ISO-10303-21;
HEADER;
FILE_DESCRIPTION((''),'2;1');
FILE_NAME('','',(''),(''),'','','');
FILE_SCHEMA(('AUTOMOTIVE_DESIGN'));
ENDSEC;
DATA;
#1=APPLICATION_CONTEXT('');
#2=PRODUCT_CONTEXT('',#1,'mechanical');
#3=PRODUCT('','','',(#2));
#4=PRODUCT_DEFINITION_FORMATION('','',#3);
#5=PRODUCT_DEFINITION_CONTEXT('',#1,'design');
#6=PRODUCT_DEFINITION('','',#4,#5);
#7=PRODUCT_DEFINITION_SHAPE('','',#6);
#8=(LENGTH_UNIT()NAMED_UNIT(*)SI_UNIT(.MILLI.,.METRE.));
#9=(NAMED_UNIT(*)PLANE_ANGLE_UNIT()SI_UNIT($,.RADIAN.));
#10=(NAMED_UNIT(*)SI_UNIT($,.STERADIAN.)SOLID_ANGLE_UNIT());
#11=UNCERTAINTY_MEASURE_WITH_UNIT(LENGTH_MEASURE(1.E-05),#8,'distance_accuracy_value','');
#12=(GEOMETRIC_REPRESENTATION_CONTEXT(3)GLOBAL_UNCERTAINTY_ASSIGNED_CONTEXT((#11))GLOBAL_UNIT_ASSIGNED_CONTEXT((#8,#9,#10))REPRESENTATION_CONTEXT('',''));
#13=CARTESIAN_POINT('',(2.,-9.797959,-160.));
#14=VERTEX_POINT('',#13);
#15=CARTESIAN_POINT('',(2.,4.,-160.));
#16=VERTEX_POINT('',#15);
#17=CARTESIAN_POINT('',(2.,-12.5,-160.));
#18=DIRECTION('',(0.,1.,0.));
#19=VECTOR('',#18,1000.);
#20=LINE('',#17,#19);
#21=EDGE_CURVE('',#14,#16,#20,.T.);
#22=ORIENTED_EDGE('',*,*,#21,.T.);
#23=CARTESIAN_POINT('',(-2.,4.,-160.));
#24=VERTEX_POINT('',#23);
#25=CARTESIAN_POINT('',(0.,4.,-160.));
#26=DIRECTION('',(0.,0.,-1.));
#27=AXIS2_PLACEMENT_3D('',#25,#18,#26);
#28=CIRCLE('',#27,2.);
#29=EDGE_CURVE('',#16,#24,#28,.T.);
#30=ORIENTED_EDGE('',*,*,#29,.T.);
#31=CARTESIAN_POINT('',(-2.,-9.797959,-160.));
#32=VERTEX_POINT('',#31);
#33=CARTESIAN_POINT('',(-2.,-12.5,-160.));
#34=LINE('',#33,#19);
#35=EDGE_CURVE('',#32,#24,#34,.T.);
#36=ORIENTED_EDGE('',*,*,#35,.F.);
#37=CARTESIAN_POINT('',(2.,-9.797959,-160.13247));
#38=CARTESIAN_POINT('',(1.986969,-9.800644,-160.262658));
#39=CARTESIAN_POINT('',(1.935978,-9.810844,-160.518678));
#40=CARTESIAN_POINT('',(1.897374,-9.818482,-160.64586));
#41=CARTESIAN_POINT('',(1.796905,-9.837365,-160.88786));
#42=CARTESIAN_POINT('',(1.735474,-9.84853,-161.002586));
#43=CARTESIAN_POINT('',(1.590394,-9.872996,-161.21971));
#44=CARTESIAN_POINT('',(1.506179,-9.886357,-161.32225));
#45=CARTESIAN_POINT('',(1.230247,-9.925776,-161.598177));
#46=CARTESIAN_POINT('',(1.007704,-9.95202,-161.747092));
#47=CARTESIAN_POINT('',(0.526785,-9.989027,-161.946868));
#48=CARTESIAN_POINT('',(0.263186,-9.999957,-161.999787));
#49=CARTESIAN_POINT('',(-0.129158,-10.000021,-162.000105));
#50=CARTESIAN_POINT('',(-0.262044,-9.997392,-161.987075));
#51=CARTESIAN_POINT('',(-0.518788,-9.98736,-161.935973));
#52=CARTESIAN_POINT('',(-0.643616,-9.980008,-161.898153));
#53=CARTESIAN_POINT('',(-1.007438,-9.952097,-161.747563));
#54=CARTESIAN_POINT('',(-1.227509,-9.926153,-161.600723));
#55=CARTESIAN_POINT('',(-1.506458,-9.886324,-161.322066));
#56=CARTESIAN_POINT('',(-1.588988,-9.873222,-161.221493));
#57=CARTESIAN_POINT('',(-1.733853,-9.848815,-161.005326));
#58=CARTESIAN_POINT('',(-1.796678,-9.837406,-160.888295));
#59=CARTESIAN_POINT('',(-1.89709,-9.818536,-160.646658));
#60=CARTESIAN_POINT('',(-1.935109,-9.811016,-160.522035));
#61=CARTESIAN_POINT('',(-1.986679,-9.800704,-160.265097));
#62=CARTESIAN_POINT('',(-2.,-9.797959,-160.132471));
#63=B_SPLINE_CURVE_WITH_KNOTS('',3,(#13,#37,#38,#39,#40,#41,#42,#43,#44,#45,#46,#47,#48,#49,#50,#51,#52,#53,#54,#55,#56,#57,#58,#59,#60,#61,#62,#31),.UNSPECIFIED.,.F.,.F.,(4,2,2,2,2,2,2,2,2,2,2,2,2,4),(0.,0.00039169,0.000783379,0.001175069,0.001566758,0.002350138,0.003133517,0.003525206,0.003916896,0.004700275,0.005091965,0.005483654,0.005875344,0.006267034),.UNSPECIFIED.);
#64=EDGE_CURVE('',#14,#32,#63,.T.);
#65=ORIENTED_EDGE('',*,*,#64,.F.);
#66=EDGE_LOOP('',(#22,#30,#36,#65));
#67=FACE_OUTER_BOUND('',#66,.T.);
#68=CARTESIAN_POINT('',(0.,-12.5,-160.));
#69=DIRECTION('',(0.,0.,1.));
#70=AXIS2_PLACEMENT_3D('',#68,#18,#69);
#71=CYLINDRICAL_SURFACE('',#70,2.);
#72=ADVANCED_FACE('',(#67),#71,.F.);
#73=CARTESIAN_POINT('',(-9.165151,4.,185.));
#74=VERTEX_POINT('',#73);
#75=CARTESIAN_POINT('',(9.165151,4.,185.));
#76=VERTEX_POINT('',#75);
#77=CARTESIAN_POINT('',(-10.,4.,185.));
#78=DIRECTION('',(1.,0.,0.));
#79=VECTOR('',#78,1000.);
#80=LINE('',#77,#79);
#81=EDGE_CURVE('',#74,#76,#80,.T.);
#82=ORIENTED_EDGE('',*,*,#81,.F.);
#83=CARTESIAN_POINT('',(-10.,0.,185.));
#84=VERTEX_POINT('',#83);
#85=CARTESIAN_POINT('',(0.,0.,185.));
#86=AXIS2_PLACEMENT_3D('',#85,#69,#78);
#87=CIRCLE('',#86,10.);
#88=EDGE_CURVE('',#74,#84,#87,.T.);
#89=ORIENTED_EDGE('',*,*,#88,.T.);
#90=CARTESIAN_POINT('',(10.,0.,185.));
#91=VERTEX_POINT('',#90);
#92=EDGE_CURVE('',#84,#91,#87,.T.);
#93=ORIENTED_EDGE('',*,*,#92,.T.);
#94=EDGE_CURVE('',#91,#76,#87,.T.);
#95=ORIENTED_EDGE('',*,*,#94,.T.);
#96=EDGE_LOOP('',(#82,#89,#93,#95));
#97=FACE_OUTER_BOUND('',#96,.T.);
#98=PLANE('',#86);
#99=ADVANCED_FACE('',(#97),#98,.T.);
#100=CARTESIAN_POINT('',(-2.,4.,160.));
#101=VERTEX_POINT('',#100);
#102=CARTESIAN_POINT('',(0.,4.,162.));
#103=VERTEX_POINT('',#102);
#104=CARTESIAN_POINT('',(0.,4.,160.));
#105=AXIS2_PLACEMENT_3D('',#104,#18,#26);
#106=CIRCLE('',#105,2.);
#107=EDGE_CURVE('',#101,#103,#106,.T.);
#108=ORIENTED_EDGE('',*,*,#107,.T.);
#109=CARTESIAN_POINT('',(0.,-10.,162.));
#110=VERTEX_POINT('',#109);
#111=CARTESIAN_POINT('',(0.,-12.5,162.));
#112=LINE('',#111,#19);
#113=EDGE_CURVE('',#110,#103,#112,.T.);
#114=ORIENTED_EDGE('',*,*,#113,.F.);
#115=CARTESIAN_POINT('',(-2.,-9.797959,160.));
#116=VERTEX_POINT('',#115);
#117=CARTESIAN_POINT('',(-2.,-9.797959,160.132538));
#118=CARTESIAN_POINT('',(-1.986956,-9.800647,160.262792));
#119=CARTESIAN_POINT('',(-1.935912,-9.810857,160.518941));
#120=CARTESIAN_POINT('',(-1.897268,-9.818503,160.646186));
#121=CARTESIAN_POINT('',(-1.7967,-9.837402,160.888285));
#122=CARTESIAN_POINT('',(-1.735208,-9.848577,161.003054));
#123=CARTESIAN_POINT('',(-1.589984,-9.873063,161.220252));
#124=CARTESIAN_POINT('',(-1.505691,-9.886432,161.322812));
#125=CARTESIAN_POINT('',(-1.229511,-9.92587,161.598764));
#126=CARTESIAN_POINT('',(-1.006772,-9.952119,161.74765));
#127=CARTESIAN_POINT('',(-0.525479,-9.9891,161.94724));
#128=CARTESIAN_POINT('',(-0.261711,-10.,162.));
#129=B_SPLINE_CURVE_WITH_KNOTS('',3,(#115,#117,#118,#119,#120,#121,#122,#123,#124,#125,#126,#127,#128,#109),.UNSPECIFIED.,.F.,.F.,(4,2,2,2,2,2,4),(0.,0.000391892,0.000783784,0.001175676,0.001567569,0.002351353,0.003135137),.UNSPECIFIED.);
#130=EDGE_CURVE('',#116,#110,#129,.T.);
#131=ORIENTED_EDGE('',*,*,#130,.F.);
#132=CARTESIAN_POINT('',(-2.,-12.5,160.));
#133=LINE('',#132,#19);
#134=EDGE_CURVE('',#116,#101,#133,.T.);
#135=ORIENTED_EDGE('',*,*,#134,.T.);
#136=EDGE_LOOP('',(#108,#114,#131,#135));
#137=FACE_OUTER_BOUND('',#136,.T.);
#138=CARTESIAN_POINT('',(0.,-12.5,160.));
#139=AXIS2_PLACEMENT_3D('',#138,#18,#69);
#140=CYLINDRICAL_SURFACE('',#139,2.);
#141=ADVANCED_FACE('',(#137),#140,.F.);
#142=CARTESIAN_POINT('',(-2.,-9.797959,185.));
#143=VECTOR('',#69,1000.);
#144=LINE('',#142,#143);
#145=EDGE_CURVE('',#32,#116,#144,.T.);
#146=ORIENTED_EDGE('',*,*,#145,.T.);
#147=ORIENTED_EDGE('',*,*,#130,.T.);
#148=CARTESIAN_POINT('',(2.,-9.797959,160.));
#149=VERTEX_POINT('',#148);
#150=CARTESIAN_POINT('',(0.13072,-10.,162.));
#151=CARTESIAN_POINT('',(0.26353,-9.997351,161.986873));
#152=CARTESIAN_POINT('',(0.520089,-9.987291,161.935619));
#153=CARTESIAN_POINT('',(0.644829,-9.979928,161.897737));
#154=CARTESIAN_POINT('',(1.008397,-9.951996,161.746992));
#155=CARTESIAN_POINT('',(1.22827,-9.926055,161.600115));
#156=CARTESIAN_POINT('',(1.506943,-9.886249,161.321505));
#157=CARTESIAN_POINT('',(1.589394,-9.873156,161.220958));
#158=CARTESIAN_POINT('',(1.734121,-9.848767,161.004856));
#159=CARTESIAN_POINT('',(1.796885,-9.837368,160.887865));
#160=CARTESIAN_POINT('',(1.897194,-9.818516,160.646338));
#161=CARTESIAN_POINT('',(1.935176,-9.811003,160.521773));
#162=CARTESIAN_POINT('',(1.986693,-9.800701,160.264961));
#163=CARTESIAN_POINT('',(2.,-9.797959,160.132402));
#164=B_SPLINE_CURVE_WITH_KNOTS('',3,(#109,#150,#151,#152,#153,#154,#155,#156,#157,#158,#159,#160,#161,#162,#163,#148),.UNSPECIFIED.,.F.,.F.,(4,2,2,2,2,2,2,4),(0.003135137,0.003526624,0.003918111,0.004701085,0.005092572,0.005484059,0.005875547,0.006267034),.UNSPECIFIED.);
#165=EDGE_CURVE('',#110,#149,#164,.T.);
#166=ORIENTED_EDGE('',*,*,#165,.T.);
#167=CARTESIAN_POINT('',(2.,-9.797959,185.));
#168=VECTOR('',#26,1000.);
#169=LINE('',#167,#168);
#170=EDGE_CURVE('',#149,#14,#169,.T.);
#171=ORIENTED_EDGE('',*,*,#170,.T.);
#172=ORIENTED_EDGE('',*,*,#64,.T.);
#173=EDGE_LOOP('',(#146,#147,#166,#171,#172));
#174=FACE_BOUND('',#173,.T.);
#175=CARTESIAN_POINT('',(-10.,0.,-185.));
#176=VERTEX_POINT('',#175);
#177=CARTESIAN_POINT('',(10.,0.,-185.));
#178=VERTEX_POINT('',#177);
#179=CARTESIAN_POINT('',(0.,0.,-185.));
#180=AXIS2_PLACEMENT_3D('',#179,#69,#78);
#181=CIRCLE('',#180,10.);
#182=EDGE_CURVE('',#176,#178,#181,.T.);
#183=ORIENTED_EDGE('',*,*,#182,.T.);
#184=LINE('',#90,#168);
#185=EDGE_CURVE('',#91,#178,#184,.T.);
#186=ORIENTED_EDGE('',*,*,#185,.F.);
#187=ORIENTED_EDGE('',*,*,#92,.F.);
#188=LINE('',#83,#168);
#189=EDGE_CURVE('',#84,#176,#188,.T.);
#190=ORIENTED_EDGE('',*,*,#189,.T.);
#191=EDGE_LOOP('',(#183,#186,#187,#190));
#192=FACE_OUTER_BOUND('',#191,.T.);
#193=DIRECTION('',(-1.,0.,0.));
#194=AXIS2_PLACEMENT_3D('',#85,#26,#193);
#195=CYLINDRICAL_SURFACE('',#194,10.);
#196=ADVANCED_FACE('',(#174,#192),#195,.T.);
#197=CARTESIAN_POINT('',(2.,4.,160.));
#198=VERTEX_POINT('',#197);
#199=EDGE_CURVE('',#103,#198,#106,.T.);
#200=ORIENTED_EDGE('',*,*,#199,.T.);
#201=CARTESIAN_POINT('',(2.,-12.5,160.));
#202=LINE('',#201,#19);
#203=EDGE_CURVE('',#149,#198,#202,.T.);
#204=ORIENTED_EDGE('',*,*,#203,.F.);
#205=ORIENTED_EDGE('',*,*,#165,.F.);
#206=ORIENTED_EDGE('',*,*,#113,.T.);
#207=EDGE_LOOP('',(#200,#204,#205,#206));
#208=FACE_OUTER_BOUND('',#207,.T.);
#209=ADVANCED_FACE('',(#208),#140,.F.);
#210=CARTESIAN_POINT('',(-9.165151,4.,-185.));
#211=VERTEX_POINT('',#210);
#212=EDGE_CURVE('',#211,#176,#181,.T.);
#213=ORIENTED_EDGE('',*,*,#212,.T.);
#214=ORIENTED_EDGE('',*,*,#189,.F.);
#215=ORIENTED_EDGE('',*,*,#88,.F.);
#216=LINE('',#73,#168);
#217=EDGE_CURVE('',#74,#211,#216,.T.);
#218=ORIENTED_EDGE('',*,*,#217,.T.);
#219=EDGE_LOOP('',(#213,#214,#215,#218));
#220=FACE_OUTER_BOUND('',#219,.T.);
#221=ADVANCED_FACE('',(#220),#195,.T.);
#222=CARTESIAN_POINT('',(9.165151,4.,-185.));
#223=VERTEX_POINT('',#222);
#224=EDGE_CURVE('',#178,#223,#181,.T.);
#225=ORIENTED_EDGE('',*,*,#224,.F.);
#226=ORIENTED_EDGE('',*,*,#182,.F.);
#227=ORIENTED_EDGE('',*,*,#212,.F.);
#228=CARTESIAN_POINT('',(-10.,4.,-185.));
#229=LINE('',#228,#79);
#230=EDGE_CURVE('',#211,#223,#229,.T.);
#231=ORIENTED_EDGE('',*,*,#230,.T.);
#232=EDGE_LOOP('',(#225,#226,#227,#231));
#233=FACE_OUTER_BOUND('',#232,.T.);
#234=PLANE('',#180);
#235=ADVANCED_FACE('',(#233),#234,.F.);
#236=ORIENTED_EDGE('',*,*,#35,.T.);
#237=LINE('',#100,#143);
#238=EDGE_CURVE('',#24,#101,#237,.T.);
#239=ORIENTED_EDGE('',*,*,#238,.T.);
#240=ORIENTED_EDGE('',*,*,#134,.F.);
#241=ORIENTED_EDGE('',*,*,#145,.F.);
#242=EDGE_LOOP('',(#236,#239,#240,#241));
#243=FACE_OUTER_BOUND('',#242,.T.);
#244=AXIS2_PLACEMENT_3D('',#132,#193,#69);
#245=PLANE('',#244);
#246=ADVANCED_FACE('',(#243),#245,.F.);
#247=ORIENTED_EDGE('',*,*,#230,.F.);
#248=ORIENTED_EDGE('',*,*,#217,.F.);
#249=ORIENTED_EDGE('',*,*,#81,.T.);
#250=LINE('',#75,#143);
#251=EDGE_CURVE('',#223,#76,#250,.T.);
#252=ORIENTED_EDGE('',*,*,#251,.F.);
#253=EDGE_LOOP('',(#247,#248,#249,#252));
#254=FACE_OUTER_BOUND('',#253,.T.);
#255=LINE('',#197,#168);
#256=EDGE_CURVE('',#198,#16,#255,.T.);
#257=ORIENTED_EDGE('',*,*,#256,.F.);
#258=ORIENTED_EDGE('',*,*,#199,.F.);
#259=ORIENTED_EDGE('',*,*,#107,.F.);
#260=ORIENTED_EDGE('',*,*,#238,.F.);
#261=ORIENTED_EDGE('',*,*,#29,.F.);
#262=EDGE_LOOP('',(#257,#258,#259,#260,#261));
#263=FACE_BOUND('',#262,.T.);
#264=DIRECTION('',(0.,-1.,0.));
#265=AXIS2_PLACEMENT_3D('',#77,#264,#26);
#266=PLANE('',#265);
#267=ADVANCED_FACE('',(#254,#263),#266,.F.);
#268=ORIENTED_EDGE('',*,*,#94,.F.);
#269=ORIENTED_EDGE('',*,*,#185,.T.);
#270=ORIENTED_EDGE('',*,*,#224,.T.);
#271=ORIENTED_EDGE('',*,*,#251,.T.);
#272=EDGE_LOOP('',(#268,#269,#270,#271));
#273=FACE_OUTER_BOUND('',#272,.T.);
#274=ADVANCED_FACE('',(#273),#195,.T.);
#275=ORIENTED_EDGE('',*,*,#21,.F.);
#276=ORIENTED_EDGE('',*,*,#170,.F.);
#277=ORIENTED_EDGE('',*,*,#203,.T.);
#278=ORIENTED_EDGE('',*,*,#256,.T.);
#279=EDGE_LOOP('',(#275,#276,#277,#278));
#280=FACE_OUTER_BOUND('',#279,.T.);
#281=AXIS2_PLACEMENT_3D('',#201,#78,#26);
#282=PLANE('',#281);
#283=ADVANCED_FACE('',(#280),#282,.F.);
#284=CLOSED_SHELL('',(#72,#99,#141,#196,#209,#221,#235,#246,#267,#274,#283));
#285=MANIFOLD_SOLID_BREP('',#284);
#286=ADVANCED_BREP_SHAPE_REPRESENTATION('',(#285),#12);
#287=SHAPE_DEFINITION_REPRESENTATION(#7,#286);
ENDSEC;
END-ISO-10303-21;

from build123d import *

# Parameters (mm, degrees)
SKETCH_3_R          = 10
EXTRUDE_3_DEPTH     = 185
CUT_EXTRUDE_1_DEPTH = 12.5
SKETCH_5_W          = 370
SKETCH_5_H          = 20
CUT_EXTRUDE_2_DEPTH = 10


with BuildPart() as part:
    # 草图3 → 凸台-拉伸3 (new, symmetric)
    with BuildSketch(Plane.XY):
        Circle(SKETCH_3_R)
    extrude(amount=EXTRUDE_3_DEPTH, both=True)

    # 草图4 → 切除-拉伸1 (cut, symmetric)
    with BuildSketch(Plane(origin=(0, 0, 0), x_dir=(1, 0, 0), z_dir=(0, 1, 0))):
        with BuildLine():
            Line((-2, -160), (-2, 160))
            ThreePointArc((-2, 160), (0, 162), (2, 160))
            Line((2, 160), (2, -160))
            ThreePointArc((2, -160), (0, -162), (-2, -160))
        make_face()
    extrude(amount=CUT_EXTRUDE_1_DEPTH, both=True, mode=Mode.SUBTRACT)

    # 草图5 → 切除-拉伸2 (cut, symmetric)
    with BuildSketch(Plane(origin=(0, 0, 0), x_dir=(0, 0, -1), z_dir=(1, 0, 0))):
        with Locations((0, 14)):
            Rectangle(SKETCH_5_W, SKETCH_5_H)
    extrude(amount=CUT_EXTRUDE_2_DEPTH, both=True, mode=Mode.SUBTRACT)


solid = part.part
